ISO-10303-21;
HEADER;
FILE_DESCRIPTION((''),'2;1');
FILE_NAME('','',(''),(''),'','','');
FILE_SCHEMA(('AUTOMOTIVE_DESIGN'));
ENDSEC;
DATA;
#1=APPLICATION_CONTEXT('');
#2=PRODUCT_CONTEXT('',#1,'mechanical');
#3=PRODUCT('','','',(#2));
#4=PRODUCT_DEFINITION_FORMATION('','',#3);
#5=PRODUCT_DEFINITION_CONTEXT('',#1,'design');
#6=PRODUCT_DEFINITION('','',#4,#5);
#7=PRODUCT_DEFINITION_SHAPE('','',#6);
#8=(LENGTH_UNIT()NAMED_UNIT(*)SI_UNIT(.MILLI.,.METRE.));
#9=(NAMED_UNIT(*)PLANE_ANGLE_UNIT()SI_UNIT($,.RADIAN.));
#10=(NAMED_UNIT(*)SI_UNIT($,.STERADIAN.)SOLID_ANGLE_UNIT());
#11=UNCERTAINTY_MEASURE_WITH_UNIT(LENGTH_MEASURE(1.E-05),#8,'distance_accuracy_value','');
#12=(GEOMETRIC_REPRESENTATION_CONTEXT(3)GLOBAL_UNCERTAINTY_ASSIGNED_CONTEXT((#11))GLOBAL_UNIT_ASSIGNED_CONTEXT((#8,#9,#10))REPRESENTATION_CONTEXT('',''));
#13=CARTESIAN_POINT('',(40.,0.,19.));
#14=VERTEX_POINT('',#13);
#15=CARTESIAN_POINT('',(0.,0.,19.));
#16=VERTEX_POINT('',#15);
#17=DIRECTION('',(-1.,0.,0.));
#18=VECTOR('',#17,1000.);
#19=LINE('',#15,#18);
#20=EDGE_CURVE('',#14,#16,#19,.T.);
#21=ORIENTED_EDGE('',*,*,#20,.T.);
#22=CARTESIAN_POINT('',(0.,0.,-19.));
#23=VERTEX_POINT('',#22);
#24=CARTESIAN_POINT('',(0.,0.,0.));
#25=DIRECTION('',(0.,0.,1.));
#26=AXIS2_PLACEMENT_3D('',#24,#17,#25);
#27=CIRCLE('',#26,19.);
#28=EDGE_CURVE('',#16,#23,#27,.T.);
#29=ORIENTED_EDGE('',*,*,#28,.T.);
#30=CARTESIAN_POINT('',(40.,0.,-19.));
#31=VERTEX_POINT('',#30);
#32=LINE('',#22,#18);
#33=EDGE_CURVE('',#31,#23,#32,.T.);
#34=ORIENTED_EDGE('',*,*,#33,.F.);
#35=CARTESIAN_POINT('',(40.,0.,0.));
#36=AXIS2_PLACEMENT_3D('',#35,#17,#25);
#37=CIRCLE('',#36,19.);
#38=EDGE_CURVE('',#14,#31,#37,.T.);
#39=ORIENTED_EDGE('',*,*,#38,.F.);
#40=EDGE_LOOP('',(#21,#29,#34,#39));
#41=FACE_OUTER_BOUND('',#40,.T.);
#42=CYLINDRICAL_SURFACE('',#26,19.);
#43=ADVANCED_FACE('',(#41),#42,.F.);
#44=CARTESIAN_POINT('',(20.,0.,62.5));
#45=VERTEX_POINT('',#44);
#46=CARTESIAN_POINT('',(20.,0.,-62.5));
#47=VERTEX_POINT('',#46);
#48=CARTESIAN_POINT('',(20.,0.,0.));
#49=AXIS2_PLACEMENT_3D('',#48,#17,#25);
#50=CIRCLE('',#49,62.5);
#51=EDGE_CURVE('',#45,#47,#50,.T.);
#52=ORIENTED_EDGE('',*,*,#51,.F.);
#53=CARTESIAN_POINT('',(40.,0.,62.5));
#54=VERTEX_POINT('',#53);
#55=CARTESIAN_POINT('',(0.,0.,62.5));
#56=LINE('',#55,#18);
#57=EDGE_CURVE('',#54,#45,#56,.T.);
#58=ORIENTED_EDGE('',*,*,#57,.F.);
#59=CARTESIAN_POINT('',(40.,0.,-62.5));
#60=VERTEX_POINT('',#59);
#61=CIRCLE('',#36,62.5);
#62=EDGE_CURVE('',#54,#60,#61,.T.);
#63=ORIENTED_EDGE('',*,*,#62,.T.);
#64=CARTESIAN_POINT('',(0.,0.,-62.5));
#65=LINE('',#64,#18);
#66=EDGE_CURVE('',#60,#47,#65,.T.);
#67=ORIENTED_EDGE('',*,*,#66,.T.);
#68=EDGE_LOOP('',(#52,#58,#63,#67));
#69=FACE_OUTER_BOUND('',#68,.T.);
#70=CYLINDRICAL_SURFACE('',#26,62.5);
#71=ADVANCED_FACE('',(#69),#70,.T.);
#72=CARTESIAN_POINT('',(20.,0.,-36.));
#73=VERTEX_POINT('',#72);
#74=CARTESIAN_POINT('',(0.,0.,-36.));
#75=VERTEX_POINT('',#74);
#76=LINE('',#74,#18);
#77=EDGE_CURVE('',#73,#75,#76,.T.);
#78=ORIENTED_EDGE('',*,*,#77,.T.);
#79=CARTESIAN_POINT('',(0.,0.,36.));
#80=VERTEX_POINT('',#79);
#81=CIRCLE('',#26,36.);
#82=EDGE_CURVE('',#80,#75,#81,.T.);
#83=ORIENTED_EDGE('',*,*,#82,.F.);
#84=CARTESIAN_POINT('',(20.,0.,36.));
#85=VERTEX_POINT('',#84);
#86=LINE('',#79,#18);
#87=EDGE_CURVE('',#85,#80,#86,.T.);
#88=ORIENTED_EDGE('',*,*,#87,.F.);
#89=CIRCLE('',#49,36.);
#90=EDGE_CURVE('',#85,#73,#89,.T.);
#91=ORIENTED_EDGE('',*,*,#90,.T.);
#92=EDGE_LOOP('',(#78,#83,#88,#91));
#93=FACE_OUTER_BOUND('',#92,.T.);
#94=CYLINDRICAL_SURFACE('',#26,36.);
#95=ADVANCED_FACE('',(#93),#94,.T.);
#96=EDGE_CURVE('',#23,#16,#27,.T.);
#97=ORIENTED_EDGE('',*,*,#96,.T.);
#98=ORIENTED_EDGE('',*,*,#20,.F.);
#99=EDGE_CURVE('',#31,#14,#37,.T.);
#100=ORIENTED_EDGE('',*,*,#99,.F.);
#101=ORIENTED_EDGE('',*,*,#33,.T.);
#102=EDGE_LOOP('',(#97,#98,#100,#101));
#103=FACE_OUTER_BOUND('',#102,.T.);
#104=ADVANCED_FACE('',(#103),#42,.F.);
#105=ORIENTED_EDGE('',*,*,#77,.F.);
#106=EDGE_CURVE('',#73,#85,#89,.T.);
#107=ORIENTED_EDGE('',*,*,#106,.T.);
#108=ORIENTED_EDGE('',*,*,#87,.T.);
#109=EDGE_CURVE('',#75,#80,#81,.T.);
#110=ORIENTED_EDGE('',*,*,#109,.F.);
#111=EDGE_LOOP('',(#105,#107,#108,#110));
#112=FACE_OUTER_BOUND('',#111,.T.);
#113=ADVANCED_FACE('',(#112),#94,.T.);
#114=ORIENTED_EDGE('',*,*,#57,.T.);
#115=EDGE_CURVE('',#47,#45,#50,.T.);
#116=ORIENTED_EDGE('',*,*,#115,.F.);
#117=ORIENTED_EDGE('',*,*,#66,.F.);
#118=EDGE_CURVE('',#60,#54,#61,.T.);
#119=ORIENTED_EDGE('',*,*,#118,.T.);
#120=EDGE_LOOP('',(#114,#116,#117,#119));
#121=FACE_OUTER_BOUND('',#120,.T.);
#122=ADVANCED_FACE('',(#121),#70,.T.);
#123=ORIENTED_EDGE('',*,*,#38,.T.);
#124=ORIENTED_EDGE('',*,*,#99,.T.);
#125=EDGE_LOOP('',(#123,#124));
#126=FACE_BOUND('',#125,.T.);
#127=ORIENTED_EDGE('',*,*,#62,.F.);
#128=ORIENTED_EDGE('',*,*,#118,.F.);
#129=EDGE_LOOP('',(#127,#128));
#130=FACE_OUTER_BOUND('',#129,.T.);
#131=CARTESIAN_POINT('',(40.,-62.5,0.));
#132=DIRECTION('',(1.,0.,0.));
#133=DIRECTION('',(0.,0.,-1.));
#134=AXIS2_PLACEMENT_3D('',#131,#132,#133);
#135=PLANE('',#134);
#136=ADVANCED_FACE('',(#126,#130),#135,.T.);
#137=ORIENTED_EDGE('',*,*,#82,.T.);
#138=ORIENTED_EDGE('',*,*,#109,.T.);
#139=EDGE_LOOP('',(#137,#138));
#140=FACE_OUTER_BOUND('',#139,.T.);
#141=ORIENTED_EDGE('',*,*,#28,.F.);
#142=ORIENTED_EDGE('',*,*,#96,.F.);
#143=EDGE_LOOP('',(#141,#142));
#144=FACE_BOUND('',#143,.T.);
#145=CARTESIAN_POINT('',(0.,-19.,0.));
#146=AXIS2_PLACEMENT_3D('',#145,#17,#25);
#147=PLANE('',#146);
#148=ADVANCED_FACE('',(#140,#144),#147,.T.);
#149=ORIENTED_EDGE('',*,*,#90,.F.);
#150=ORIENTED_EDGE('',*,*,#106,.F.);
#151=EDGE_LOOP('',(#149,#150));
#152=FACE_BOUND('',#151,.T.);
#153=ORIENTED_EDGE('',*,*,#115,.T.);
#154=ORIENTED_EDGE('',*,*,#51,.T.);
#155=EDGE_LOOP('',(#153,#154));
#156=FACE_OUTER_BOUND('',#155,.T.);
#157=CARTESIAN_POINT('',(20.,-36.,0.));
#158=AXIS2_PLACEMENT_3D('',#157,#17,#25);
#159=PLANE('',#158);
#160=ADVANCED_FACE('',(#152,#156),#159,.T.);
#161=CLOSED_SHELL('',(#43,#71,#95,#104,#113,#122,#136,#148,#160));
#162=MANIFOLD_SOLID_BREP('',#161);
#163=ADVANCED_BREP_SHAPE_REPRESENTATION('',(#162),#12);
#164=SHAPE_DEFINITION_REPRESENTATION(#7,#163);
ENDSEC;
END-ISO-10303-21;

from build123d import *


with BuildPart() as part:
    # Sketch1 → Revolve1 (revolve)
    with BuildSketch(Plane.XY, mode=Mode.PRIVATE) as revolve1_sk:
        Polygon((0, -19), (0, -36), (20, -36), (20, -62.5), (40, -62.5), (40, -19), align=None)
    revolve(revolve1_sk.sketch.rotate(Axis((0, 0, 0), (1, 0, 0)), 270), axis=Axis((0, 0, 0), (1, 0, 0)))


solid = part.part
